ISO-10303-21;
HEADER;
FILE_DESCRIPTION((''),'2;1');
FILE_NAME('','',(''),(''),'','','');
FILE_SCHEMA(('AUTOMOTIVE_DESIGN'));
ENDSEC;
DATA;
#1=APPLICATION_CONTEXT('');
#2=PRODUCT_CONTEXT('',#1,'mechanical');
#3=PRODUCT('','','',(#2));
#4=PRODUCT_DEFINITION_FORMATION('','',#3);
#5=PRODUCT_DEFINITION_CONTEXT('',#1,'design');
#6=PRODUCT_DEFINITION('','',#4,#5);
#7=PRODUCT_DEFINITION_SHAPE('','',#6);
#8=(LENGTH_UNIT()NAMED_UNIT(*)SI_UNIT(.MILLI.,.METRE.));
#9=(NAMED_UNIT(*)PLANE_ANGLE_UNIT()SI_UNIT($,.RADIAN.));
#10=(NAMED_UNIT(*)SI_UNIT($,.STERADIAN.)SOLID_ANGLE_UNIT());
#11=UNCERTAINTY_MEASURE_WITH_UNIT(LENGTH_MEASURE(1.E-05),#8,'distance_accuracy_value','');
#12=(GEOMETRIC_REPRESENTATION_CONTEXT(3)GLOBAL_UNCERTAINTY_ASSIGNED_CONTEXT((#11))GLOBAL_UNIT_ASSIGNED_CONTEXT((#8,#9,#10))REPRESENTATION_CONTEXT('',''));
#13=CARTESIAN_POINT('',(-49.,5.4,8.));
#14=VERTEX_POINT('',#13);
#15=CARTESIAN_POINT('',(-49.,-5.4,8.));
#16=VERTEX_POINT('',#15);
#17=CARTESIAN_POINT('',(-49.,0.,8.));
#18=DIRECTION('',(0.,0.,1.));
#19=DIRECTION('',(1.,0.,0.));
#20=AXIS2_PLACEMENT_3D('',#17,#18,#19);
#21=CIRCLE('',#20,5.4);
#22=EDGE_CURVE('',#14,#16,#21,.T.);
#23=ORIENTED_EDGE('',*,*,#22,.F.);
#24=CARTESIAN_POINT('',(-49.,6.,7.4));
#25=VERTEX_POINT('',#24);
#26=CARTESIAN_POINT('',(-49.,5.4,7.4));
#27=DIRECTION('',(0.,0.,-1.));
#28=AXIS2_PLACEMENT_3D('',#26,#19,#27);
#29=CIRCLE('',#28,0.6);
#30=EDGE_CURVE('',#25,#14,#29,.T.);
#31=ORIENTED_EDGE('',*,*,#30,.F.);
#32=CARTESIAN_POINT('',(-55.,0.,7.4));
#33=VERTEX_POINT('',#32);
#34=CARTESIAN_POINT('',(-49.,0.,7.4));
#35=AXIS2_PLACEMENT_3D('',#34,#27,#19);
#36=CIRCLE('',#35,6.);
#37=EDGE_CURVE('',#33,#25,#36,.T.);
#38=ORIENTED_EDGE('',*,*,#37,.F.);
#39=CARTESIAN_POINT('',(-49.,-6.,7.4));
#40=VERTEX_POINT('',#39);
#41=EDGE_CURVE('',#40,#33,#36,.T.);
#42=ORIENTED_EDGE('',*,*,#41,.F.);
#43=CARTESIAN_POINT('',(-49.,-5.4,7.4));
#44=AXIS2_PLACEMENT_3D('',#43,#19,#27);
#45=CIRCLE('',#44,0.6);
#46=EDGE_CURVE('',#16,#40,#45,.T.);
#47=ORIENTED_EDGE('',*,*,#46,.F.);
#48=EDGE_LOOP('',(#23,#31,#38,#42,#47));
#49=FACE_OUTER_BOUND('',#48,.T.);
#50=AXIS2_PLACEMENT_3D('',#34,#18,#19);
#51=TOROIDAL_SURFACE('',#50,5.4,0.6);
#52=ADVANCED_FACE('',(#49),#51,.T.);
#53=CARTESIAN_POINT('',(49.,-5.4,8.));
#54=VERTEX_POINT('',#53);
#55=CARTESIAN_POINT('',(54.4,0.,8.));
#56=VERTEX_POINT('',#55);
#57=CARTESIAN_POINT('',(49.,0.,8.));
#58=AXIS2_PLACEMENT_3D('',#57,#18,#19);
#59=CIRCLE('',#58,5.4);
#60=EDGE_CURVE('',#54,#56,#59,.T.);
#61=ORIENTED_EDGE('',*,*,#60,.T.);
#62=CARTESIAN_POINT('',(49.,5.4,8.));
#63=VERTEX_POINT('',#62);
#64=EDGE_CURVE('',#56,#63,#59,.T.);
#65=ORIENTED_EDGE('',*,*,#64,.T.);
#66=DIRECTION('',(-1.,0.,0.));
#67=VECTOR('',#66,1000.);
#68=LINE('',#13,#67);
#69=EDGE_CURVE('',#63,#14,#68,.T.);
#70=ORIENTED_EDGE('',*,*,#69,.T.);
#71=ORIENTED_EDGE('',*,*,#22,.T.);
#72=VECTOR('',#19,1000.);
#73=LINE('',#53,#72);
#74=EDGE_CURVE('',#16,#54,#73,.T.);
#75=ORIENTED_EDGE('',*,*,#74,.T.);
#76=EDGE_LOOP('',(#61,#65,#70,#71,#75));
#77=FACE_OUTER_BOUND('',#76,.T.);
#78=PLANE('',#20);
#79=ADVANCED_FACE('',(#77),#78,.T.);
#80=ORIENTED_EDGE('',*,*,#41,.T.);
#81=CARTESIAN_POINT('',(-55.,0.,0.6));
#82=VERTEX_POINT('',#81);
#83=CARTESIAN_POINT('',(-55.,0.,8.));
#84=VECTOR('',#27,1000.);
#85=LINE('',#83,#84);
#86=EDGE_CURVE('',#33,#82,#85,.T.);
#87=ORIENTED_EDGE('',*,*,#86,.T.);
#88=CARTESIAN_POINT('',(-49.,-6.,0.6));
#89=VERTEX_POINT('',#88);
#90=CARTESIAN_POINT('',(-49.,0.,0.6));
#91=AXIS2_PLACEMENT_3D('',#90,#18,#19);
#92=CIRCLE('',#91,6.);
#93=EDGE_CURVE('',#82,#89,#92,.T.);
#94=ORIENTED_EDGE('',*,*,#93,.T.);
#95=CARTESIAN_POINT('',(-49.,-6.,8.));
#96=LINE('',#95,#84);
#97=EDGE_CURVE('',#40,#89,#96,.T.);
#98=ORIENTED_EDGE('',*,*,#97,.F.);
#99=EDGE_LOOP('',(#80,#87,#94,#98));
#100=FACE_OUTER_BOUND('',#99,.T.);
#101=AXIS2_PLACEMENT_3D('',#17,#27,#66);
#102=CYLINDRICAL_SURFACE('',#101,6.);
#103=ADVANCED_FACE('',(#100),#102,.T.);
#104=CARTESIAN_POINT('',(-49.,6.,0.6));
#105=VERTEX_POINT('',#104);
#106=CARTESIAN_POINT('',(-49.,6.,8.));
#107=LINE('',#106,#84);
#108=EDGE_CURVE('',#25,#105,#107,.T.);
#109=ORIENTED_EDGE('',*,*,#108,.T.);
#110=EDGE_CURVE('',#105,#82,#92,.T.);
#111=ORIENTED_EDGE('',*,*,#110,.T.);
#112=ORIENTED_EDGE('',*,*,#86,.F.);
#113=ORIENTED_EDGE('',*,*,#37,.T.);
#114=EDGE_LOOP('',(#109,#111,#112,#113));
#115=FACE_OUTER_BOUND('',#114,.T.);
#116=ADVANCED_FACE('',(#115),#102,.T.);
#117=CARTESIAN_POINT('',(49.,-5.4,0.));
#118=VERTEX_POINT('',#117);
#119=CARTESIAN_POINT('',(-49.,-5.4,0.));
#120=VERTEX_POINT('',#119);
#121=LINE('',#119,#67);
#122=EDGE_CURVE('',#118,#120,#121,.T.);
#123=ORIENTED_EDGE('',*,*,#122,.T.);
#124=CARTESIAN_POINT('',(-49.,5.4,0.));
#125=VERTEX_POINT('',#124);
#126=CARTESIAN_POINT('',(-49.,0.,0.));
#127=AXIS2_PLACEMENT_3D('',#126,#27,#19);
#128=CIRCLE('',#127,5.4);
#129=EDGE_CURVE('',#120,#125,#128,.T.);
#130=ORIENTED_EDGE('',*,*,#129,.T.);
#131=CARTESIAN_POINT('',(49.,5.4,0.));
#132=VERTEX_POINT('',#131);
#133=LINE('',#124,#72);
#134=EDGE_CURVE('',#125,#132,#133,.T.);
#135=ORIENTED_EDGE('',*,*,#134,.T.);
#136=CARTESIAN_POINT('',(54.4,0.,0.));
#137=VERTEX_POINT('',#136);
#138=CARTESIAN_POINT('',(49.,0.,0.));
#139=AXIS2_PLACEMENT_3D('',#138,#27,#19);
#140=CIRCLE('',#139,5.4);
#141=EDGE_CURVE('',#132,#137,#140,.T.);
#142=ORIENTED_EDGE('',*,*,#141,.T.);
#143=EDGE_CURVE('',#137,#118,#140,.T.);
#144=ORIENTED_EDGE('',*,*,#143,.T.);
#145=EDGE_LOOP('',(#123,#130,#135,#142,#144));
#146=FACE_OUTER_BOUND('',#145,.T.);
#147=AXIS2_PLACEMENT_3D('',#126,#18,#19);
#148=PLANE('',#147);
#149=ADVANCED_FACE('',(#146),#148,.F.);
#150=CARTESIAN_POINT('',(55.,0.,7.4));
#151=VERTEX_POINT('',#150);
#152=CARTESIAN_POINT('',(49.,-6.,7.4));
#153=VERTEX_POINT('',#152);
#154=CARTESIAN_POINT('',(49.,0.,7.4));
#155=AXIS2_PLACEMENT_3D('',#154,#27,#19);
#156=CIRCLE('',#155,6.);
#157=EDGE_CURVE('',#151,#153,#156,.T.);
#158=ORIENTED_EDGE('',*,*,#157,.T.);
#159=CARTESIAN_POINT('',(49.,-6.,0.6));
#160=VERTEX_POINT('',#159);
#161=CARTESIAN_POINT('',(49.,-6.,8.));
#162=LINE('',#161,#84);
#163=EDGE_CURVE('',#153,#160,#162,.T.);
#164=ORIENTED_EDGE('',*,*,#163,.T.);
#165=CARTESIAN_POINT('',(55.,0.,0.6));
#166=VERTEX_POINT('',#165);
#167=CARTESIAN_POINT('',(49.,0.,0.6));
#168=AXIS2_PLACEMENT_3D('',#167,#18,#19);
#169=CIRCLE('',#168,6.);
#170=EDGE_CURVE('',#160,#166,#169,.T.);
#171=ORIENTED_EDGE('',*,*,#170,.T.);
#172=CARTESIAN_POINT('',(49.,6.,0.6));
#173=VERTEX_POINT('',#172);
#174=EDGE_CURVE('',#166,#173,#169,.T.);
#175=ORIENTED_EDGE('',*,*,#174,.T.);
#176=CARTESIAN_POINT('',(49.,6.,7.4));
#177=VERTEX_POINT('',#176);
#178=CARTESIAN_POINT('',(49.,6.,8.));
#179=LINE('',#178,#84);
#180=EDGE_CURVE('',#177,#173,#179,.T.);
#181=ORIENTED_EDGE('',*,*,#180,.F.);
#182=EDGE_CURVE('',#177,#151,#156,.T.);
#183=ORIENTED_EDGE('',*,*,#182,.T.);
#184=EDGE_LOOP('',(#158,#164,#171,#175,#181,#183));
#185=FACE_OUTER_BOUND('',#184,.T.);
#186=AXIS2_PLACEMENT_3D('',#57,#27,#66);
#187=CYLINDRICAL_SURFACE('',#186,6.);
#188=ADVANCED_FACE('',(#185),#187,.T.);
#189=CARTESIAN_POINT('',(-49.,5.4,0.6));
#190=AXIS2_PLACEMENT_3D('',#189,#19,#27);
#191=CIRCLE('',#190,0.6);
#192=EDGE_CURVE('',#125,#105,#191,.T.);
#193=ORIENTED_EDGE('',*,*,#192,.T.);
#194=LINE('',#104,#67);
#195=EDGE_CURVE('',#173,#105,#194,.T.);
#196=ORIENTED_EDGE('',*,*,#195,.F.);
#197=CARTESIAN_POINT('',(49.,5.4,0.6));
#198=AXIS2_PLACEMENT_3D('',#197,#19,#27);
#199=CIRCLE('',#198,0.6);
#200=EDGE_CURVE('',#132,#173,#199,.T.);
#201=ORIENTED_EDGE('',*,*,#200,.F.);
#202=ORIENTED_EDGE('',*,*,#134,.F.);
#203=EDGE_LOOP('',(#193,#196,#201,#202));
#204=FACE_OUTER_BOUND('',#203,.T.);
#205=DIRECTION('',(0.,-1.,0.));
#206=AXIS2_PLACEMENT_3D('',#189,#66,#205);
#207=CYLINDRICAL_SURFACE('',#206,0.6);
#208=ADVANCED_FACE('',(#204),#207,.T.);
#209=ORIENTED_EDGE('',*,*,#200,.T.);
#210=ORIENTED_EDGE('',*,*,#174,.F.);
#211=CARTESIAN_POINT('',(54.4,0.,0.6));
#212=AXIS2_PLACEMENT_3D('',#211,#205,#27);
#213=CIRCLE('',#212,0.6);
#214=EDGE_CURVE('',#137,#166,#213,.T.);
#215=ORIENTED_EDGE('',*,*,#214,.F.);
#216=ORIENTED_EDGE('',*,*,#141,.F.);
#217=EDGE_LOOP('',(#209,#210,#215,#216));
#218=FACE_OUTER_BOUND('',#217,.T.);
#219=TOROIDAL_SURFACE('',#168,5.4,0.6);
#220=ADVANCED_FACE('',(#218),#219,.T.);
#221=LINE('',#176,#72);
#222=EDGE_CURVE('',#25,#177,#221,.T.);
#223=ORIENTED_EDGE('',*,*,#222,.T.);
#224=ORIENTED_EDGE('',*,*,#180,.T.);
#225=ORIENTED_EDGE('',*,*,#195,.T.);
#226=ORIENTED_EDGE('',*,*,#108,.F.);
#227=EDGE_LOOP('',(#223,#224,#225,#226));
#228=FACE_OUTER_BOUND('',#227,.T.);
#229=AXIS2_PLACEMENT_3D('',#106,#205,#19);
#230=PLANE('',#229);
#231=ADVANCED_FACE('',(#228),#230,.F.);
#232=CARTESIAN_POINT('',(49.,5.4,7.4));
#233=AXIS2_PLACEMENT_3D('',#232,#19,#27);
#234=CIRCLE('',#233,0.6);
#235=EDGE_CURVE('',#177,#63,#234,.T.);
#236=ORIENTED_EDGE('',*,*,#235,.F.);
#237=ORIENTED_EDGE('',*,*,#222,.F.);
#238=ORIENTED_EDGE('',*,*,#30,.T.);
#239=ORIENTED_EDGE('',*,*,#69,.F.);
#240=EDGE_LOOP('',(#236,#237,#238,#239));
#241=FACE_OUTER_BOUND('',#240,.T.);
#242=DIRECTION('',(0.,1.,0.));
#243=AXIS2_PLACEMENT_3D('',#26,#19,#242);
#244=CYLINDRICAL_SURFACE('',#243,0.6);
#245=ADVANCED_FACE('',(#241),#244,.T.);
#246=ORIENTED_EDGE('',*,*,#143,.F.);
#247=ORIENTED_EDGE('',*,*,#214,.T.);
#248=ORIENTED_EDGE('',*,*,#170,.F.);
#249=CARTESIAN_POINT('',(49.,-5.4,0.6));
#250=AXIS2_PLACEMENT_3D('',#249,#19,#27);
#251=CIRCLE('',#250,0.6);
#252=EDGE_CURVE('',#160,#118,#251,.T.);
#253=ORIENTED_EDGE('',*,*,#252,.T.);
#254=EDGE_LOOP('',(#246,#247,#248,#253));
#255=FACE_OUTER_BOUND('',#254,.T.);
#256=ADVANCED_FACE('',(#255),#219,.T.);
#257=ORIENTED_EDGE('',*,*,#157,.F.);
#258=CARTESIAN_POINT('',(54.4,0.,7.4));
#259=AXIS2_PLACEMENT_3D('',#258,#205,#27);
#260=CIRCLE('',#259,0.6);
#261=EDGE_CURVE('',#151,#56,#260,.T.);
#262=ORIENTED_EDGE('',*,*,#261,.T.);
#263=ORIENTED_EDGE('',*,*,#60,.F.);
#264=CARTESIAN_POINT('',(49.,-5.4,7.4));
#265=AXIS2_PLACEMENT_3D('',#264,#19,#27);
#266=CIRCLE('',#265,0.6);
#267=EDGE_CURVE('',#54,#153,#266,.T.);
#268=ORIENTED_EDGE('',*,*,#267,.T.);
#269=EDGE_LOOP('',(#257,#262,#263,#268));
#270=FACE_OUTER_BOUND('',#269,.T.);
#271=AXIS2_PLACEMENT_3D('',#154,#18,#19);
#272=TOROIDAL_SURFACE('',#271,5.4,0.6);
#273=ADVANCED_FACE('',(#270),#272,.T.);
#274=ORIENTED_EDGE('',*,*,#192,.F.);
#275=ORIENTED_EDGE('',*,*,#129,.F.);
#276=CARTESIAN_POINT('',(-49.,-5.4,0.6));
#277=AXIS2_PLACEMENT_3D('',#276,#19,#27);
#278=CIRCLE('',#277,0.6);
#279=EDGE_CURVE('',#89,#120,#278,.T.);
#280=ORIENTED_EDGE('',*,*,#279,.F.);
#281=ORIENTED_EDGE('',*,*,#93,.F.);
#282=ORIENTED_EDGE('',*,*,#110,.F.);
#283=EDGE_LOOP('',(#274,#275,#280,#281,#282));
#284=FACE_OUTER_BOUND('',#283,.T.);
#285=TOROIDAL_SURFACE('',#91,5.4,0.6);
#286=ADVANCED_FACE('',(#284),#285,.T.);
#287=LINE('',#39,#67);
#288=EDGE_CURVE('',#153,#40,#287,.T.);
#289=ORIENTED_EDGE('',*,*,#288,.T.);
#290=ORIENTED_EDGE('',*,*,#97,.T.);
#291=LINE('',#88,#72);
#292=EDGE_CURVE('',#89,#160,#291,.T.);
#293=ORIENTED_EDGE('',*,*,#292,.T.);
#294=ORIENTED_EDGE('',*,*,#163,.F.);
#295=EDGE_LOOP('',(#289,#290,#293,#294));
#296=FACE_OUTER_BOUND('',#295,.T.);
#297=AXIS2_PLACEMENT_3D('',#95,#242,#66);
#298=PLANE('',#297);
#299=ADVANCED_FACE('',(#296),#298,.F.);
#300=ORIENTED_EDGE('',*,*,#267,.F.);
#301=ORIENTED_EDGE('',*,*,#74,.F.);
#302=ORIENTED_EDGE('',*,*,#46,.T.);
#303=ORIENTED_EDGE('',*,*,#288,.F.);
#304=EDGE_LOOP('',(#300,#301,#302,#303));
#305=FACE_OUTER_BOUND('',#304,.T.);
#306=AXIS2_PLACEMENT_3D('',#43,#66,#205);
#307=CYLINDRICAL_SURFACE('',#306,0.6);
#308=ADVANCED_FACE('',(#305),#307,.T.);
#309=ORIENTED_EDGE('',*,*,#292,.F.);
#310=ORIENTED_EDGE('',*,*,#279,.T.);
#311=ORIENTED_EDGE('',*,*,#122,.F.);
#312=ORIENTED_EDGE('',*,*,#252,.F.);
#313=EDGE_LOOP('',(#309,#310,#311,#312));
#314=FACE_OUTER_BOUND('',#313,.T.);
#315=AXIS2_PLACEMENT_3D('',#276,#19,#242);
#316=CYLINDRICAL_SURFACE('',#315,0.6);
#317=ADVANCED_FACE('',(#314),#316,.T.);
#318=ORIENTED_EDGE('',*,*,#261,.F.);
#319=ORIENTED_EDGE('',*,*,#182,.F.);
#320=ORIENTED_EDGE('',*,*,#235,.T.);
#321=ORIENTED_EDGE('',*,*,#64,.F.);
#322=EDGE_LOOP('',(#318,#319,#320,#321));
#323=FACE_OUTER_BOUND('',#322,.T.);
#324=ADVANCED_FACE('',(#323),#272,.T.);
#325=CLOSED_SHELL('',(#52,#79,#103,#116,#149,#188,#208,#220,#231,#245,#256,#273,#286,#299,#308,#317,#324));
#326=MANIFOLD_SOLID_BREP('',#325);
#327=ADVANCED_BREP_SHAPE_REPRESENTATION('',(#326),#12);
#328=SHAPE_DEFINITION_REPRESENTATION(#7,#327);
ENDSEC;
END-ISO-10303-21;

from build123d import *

# Parameters (mm, degrees)
EXTRUDE_523_DEPTH = 8
FILLET_1_R        = 0.6


with BuildPart() as part:
    # 草图1 → Extrude 523 (new body)
    with BuildSketch(Plane.XY):
        with BuildLine():
            Line((-49, 6), (49, 6))
            ThreePointArc((49, 6), (55, 0), (49, -6))
            Line((49, -6), (-49, -6))
            ThreePointArc((-49, -6), (-55, 0), (-49, 6))
        make_face()
    extrude(amount=EXTRUDE_523_DEPTH)

    # 圆角1
    fillet_1_edges = [part.edges().sort_by_distance(p)[0] for p in [
        (55, 0, 8),
        (0, 6, 8),
        (-55, 0, 8),
        (0, 6, 0),
        (55, 0, 0),
        (0, -6, 0),
        (-55, 0, 0),
        (0, -6, 8),
    ]]
    fillet(fillet_1_edges, radius=FILLET_1_R)


solid = part.part
